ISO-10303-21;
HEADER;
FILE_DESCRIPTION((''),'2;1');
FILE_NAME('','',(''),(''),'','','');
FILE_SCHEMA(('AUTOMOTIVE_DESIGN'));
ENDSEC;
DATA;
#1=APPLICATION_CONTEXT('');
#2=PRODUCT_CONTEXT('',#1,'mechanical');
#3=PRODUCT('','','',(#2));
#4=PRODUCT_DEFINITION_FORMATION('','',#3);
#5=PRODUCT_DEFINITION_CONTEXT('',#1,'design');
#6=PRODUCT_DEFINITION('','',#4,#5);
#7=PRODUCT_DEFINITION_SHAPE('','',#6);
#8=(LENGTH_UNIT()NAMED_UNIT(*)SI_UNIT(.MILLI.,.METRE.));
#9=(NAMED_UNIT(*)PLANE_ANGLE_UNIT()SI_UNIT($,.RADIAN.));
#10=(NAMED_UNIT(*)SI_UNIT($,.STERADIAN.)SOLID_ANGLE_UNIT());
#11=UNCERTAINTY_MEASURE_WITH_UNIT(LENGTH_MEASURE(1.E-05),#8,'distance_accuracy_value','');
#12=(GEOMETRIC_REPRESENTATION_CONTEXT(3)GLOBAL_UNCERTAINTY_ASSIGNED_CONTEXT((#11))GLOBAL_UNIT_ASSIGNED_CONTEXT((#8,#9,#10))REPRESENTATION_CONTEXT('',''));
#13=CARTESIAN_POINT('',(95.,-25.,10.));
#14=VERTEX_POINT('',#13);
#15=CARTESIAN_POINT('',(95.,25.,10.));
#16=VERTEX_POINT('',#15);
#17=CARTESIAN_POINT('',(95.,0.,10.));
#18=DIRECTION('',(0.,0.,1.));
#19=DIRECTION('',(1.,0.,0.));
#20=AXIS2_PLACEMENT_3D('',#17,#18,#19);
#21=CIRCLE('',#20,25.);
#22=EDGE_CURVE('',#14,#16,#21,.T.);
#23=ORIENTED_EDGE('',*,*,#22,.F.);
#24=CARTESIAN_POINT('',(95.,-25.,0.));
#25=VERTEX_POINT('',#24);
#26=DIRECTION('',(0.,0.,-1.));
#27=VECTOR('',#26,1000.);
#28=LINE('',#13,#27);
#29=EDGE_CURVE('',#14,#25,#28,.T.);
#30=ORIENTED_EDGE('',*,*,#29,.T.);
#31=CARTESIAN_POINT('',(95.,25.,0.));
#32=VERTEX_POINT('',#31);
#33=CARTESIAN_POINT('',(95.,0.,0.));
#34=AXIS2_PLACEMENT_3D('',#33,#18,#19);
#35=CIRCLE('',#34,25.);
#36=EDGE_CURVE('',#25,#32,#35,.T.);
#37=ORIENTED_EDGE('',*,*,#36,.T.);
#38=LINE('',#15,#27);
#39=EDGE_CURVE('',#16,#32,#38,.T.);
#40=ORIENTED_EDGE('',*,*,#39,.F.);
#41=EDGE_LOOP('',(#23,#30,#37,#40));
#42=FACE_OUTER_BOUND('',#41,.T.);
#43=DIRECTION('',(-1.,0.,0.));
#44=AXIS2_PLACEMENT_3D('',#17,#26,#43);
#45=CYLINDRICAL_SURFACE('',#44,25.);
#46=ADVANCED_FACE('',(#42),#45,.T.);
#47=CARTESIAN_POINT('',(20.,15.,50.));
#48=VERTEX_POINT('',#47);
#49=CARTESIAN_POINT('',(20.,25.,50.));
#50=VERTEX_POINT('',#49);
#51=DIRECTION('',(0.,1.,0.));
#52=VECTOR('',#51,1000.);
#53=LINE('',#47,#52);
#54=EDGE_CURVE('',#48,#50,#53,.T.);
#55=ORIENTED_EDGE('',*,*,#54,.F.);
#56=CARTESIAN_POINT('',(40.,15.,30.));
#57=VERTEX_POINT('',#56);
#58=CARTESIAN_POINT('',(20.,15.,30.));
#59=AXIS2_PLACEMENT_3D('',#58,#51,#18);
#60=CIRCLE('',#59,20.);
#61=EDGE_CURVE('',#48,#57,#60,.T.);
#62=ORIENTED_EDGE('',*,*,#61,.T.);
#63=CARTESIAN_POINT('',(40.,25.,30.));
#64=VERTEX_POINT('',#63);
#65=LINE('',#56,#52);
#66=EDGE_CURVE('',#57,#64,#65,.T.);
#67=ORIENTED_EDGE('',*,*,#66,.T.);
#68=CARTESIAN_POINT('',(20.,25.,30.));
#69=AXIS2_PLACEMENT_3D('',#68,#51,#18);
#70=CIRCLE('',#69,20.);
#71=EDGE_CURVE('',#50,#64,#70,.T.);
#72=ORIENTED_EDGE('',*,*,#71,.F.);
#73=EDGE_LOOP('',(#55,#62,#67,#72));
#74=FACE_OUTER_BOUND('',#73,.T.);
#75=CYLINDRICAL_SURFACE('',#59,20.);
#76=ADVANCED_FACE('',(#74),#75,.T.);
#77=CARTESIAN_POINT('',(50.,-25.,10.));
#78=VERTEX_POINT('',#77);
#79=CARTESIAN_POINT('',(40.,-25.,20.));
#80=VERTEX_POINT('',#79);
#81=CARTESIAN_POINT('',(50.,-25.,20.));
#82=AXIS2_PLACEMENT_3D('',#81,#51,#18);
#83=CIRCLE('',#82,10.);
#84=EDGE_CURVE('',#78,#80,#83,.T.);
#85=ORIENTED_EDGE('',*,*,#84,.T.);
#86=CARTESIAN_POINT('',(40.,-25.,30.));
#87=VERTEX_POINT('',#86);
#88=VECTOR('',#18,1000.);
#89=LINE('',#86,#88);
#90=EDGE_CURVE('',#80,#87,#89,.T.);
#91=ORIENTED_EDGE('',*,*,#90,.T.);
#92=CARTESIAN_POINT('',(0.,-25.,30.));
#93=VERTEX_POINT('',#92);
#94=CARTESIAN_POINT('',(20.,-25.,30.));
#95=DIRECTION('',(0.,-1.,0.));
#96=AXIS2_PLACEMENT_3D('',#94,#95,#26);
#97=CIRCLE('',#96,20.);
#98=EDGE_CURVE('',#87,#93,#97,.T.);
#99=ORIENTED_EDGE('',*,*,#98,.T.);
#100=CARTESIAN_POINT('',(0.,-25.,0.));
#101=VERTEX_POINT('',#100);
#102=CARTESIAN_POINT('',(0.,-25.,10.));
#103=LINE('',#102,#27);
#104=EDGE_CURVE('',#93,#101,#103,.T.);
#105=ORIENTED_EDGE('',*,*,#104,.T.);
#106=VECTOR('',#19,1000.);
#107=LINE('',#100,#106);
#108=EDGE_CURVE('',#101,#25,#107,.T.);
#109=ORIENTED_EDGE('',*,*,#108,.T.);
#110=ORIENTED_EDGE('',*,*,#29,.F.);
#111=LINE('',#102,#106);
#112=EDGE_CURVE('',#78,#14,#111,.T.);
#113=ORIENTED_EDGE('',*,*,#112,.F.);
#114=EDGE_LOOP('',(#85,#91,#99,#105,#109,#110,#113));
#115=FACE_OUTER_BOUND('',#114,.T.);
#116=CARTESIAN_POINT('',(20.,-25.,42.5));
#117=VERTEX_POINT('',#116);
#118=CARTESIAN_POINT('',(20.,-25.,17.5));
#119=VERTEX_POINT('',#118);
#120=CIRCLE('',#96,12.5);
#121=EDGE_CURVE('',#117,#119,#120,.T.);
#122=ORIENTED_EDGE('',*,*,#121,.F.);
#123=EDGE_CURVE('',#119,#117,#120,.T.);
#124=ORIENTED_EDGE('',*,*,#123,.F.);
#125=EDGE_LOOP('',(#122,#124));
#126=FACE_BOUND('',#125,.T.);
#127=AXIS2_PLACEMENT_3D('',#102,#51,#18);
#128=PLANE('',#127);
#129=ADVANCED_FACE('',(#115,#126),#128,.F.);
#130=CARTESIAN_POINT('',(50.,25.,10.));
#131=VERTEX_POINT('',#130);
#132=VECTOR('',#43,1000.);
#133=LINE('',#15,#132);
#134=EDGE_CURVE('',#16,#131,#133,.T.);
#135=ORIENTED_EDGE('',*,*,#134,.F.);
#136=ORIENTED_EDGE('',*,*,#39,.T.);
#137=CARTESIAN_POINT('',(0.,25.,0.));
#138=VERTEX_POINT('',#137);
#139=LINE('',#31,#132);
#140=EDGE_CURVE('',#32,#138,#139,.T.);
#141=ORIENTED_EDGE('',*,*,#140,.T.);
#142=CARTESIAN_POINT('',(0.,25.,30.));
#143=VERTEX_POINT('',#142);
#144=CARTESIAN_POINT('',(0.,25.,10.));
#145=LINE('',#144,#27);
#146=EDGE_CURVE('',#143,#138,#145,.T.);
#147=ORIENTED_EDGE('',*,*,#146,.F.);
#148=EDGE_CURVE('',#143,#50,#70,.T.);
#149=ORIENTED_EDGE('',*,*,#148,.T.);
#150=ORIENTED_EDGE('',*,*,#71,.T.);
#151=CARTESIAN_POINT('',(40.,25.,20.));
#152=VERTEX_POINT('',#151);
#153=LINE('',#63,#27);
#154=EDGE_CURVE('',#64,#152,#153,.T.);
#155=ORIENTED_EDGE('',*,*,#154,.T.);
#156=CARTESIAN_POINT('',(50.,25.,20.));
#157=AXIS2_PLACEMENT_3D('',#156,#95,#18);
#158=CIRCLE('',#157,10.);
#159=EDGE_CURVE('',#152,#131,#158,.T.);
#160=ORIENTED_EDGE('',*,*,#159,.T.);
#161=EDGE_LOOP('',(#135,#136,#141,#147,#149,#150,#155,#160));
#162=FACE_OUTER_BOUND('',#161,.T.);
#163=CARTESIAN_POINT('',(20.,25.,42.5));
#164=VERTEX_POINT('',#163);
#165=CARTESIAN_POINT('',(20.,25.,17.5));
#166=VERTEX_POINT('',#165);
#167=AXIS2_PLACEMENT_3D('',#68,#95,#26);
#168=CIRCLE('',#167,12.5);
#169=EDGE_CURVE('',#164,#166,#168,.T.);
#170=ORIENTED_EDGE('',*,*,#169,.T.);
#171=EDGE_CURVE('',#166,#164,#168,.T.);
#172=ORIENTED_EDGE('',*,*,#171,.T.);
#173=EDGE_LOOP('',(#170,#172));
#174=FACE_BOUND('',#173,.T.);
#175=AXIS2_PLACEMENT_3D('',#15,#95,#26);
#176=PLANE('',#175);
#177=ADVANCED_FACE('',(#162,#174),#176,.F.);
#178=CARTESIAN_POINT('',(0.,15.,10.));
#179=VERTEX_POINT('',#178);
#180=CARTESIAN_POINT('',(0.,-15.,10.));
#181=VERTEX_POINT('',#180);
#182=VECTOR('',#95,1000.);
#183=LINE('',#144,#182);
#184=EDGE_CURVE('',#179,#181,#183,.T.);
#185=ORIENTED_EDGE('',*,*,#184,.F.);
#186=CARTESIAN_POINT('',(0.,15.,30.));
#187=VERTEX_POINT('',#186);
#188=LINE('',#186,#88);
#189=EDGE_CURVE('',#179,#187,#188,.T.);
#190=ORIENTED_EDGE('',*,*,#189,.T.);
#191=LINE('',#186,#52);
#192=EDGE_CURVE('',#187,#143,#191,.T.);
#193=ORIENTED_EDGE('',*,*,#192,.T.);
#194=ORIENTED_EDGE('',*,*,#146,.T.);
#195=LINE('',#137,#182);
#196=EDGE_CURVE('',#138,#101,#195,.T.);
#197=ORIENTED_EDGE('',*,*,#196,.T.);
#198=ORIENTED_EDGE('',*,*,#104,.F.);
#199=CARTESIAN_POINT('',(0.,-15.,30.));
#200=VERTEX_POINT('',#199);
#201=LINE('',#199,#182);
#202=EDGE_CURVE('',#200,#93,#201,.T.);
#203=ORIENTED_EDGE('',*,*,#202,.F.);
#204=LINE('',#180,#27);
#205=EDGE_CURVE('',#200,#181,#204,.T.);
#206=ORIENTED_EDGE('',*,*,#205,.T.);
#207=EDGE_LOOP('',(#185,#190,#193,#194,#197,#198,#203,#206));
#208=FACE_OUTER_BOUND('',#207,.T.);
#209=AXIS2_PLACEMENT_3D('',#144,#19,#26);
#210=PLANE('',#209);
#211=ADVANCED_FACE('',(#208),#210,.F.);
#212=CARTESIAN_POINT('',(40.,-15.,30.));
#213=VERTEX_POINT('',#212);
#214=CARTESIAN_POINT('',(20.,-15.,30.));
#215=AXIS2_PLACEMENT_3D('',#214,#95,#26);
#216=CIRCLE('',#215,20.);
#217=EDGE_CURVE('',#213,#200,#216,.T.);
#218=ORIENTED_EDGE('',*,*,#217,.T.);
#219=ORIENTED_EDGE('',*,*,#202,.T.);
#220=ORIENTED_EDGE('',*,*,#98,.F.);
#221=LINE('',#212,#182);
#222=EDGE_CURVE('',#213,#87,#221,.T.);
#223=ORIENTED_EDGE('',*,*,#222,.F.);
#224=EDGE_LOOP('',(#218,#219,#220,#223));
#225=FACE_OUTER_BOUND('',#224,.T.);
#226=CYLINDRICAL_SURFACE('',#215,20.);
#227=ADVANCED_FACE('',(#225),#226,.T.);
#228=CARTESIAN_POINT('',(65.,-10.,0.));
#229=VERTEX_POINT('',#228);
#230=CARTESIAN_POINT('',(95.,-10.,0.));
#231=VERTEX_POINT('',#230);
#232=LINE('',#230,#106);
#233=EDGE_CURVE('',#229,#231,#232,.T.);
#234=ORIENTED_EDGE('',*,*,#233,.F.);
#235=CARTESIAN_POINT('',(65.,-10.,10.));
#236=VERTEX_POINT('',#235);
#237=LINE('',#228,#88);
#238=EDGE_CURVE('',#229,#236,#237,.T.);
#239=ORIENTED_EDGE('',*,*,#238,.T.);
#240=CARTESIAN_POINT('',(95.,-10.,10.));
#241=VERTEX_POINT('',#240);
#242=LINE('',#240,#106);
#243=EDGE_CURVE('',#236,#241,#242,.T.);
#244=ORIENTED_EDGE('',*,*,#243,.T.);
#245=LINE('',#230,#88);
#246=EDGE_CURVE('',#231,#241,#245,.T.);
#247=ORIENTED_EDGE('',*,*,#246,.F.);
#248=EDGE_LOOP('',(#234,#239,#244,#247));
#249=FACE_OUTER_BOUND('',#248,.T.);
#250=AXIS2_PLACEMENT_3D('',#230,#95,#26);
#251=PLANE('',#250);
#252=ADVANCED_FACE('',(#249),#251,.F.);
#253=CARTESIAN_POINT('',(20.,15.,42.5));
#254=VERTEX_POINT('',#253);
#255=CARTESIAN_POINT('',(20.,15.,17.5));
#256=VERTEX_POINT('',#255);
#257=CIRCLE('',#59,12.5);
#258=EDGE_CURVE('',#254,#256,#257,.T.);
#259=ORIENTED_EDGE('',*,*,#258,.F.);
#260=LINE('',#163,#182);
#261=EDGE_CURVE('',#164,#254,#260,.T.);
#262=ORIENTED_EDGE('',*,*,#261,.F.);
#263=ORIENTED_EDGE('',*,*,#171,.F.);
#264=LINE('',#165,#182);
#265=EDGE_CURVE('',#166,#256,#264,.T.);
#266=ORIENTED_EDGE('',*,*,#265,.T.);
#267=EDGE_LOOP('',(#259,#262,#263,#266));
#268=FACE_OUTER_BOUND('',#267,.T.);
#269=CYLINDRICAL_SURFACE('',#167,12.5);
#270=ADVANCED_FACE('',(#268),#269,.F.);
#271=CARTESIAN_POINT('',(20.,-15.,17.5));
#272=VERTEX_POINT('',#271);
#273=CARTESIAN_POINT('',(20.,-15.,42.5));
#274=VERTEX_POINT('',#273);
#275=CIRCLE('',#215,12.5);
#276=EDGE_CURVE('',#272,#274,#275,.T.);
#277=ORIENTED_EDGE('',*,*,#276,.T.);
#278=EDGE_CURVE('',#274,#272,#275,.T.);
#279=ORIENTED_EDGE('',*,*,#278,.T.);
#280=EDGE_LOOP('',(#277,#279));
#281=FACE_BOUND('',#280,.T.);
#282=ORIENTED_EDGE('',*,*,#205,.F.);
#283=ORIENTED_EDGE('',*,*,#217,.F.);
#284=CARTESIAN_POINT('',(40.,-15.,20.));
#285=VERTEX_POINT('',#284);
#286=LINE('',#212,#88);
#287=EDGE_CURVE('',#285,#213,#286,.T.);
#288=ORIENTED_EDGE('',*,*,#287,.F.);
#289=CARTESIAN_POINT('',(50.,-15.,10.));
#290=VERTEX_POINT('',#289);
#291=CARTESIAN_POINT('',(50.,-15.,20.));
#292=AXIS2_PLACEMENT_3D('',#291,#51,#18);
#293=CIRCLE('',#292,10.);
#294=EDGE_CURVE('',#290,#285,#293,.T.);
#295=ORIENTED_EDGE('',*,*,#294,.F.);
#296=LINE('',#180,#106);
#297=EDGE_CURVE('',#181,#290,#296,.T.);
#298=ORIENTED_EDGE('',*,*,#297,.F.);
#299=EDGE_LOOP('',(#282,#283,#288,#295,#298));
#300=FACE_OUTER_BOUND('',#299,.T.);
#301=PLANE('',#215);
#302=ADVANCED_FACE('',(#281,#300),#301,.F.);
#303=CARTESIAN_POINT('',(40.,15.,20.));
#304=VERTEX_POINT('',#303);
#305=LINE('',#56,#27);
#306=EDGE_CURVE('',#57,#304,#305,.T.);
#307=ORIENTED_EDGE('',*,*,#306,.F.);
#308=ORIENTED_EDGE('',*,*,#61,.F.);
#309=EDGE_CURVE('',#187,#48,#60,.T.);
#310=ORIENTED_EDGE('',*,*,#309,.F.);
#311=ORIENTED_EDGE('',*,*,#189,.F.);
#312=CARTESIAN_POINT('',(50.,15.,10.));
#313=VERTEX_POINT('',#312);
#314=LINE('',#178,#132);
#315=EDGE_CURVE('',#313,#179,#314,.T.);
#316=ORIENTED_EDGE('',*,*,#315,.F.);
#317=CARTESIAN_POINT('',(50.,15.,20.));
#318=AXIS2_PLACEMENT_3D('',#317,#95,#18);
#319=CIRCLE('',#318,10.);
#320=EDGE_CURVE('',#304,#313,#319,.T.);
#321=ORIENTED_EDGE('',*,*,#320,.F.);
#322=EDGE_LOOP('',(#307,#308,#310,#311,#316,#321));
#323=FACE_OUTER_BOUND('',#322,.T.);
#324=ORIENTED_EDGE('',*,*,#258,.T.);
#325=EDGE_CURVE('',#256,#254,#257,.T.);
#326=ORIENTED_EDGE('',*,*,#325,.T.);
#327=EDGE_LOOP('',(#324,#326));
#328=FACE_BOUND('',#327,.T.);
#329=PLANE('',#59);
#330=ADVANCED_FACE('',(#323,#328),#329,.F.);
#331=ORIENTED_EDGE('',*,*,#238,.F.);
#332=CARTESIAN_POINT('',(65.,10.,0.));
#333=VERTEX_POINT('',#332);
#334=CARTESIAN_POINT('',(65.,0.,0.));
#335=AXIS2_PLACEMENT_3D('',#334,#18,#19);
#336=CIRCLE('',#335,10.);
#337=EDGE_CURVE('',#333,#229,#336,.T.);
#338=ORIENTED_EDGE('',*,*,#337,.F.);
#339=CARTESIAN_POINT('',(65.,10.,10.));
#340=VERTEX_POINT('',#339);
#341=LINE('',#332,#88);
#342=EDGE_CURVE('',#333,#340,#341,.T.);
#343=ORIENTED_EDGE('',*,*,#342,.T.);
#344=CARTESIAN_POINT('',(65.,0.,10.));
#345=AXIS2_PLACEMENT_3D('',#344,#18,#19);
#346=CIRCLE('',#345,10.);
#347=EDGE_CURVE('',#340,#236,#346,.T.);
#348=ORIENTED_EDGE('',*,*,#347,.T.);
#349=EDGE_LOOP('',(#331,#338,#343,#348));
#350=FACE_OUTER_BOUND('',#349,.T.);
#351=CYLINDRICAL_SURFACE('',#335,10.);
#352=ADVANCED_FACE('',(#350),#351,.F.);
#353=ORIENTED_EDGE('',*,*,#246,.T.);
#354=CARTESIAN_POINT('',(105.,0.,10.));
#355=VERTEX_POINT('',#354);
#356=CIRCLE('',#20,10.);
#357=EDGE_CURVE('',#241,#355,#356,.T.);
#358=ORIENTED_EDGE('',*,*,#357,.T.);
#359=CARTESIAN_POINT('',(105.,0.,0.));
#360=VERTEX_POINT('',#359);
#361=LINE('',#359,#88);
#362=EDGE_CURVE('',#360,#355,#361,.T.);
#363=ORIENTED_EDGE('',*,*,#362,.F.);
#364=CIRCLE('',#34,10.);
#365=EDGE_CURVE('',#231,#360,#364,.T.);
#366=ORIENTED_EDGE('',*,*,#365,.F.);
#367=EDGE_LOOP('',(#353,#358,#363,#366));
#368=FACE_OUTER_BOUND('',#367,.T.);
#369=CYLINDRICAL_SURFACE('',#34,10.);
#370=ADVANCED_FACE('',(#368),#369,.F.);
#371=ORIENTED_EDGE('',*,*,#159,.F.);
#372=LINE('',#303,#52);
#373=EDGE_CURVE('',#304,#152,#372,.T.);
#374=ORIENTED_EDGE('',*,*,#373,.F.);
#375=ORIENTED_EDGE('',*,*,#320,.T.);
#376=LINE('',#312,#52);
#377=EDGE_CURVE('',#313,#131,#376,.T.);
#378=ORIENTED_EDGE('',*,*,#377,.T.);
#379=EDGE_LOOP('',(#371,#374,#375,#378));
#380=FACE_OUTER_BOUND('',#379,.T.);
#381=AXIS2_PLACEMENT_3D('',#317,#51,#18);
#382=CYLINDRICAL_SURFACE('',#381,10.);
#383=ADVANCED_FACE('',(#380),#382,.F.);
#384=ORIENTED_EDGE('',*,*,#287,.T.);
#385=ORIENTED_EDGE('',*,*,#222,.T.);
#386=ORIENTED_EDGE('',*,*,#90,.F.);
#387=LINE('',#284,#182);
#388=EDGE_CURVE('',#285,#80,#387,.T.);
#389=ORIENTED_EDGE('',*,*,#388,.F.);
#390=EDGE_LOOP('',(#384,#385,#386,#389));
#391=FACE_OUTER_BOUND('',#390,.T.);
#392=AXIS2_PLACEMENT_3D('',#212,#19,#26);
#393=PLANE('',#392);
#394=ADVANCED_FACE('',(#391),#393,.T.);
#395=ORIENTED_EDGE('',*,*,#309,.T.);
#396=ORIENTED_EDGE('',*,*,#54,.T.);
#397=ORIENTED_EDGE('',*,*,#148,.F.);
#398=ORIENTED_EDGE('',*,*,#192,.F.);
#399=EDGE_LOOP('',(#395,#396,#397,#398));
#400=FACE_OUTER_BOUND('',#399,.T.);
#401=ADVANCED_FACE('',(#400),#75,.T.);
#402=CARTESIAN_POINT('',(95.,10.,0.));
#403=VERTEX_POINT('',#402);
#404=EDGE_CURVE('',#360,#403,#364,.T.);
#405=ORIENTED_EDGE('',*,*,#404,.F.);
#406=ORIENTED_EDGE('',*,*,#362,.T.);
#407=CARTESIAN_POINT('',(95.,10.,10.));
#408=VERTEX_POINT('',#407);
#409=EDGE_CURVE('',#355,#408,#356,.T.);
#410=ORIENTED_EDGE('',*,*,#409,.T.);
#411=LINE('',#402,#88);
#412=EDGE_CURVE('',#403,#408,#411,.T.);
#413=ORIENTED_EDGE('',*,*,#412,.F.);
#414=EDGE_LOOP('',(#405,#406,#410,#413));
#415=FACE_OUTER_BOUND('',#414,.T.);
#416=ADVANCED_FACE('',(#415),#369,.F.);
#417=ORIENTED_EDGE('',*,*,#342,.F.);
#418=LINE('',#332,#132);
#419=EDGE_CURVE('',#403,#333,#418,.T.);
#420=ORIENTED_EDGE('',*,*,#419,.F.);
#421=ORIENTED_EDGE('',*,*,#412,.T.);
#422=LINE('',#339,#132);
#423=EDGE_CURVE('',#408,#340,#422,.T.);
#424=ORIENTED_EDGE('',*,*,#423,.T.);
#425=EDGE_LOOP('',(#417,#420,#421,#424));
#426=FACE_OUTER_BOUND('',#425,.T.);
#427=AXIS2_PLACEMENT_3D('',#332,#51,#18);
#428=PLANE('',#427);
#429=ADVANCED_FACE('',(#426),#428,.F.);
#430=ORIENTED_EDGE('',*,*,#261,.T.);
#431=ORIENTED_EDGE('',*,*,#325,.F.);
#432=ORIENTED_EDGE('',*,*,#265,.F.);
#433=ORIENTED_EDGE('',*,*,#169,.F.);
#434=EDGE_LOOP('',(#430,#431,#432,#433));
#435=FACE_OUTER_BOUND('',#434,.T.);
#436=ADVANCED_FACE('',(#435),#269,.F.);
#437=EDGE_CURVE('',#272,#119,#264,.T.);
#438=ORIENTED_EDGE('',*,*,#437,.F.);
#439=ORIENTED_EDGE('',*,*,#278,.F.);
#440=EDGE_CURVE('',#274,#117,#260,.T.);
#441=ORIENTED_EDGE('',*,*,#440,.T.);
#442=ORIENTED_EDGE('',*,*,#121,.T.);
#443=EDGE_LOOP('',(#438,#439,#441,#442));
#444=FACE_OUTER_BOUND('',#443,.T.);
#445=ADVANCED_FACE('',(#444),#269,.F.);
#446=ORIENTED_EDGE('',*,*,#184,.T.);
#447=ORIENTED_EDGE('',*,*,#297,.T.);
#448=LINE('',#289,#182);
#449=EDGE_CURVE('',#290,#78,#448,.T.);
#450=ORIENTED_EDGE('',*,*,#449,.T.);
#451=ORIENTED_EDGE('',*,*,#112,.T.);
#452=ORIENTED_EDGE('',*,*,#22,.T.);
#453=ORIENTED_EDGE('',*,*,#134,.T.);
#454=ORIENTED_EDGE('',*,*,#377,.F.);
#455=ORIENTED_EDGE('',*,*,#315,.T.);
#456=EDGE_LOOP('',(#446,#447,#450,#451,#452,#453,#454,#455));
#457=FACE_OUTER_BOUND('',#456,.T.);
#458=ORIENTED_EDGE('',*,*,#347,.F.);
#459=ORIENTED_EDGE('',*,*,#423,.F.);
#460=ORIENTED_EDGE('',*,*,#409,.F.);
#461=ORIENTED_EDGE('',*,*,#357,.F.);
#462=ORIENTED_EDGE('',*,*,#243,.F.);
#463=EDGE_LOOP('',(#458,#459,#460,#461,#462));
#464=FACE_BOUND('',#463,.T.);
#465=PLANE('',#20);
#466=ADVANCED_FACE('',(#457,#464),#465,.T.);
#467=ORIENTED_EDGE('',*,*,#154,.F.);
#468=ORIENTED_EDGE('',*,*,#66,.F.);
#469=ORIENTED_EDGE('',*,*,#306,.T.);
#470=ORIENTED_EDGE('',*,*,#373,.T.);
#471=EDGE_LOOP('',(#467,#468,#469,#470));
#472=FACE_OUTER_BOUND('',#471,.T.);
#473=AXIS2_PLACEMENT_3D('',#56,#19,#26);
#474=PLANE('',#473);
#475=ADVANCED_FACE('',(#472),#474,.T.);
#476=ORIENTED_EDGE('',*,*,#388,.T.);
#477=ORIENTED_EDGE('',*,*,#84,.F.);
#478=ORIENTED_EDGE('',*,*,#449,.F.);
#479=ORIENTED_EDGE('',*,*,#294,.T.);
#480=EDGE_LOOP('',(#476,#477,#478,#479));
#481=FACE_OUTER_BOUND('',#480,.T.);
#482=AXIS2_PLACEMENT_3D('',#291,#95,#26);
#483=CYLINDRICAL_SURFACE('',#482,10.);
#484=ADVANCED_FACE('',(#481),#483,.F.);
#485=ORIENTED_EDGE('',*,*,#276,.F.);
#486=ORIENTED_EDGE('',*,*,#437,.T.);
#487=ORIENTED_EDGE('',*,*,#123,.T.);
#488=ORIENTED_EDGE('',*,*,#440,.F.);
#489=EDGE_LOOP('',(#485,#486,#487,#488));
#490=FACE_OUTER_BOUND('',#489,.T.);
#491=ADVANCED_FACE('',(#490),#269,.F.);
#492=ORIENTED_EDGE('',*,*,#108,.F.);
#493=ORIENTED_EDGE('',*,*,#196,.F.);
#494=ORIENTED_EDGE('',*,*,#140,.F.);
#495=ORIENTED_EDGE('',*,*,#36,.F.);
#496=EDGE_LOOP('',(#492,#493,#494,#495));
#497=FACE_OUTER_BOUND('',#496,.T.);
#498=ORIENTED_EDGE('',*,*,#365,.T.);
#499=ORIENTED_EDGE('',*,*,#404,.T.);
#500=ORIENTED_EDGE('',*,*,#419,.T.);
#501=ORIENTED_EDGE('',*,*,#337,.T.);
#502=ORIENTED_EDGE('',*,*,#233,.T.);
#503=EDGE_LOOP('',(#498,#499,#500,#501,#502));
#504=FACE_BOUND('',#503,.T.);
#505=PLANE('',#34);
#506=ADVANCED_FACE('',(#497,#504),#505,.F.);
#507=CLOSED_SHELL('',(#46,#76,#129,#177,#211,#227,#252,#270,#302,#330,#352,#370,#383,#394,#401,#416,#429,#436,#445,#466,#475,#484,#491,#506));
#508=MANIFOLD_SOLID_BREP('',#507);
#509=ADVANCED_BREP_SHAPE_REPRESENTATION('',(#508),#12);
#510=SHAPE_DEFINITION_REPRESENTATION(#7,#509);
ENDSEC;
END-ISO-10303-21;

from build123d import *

# Parameters (mm, degrees)
BASE_PLATE_DEPTH  = 10
SLOT_CUT_DEPTH    = 10
LUG_1_DEPTH       = 10
LUG_START         = -10
LUG_2_DEPTH       = 10
PIN_HOLE_SKETCH_R = 12.5
PIN_HOLE_25_DEPTH = 50


with BuildPart() as part:
    # Base Plate Sketch → Base Plate (new body)
    with BuildSketch(Plane.XY):
        with BuildLine():
            Line((95, 25), (0, 25))
            Line((0, 25), (0, -25))
            Line((0, -25), (95, -25))
            ThreePointArc((95, -25), (120, 0), (95, 25))
        make_face()
    extrude(amount=BASE_PLATE_DEPTH)

    # Slot Sketch → Slot Cut (cut)
    with BuildSketch(Plane.XY.offset(10)):
        with BuildLine():
            Line((65, 10), (95, 10))
            ThreePointArc((95, 10), (105, 0), (95, -10))
            Line((95, -10), (65, -10))
            ThreePointArc((65, -10), (55, 0), (65, 10))
        make_face()
    extrude(amount=-SLOT_CUT_DEPTH, mode=Mode.SUBTRACT)

    # Lug 1 Sketch → Lug 1 (add)
    with BuildSketch(Plane.XZ.offset(25)):
        with BuildLine():
            Line((0, 10), (0, 30))
            ThreePointArc((0, 30), (20, 50), (40, 30))
            Line((40, 30), (40, 20))
            ThreePointArc((40, 20), (42.928932188, 12.928932188), (50, 10))
            Line((50, 10), (0, 10))
        make_face()
    extrude(amount=-LUG_1_DEPTH)

    # Lug 2 Sketch → Lug 2 (add)
    with BuildSketch(Plane(origin=(0, 25, 0), x_dir=(1, 0, 0), z_dir=(0, 1, 0)).offset(LUG_START)):
        with BuildLine():
            Line((0, -30), (0, -10))
            Line((0, -10), (50, -10))
            ThreePointArc((50, -10), (42.928932188, -12.928932188), (40, -20))
            Line((40, -20), (40, -30))
            ThreePointArc((40, -30), (20, -50), (0, -30))
        make_face()
    extrude(amount=LUG_2_DEPTH)

    # Pin Hole Sketch → Pin Hole Ø25 (cut)
    with BuildSketch(Plane.XZ.offset(25)):
        with Locations(Location((20, 30, 0), (0, 0, 270))):
            Circle(PIN_HOLE_SKETCH_R)
    extrude(amount=-PIN_HOLE_25_DEPTH, mode=Mode.SUBTRACT)


solid = part.part
